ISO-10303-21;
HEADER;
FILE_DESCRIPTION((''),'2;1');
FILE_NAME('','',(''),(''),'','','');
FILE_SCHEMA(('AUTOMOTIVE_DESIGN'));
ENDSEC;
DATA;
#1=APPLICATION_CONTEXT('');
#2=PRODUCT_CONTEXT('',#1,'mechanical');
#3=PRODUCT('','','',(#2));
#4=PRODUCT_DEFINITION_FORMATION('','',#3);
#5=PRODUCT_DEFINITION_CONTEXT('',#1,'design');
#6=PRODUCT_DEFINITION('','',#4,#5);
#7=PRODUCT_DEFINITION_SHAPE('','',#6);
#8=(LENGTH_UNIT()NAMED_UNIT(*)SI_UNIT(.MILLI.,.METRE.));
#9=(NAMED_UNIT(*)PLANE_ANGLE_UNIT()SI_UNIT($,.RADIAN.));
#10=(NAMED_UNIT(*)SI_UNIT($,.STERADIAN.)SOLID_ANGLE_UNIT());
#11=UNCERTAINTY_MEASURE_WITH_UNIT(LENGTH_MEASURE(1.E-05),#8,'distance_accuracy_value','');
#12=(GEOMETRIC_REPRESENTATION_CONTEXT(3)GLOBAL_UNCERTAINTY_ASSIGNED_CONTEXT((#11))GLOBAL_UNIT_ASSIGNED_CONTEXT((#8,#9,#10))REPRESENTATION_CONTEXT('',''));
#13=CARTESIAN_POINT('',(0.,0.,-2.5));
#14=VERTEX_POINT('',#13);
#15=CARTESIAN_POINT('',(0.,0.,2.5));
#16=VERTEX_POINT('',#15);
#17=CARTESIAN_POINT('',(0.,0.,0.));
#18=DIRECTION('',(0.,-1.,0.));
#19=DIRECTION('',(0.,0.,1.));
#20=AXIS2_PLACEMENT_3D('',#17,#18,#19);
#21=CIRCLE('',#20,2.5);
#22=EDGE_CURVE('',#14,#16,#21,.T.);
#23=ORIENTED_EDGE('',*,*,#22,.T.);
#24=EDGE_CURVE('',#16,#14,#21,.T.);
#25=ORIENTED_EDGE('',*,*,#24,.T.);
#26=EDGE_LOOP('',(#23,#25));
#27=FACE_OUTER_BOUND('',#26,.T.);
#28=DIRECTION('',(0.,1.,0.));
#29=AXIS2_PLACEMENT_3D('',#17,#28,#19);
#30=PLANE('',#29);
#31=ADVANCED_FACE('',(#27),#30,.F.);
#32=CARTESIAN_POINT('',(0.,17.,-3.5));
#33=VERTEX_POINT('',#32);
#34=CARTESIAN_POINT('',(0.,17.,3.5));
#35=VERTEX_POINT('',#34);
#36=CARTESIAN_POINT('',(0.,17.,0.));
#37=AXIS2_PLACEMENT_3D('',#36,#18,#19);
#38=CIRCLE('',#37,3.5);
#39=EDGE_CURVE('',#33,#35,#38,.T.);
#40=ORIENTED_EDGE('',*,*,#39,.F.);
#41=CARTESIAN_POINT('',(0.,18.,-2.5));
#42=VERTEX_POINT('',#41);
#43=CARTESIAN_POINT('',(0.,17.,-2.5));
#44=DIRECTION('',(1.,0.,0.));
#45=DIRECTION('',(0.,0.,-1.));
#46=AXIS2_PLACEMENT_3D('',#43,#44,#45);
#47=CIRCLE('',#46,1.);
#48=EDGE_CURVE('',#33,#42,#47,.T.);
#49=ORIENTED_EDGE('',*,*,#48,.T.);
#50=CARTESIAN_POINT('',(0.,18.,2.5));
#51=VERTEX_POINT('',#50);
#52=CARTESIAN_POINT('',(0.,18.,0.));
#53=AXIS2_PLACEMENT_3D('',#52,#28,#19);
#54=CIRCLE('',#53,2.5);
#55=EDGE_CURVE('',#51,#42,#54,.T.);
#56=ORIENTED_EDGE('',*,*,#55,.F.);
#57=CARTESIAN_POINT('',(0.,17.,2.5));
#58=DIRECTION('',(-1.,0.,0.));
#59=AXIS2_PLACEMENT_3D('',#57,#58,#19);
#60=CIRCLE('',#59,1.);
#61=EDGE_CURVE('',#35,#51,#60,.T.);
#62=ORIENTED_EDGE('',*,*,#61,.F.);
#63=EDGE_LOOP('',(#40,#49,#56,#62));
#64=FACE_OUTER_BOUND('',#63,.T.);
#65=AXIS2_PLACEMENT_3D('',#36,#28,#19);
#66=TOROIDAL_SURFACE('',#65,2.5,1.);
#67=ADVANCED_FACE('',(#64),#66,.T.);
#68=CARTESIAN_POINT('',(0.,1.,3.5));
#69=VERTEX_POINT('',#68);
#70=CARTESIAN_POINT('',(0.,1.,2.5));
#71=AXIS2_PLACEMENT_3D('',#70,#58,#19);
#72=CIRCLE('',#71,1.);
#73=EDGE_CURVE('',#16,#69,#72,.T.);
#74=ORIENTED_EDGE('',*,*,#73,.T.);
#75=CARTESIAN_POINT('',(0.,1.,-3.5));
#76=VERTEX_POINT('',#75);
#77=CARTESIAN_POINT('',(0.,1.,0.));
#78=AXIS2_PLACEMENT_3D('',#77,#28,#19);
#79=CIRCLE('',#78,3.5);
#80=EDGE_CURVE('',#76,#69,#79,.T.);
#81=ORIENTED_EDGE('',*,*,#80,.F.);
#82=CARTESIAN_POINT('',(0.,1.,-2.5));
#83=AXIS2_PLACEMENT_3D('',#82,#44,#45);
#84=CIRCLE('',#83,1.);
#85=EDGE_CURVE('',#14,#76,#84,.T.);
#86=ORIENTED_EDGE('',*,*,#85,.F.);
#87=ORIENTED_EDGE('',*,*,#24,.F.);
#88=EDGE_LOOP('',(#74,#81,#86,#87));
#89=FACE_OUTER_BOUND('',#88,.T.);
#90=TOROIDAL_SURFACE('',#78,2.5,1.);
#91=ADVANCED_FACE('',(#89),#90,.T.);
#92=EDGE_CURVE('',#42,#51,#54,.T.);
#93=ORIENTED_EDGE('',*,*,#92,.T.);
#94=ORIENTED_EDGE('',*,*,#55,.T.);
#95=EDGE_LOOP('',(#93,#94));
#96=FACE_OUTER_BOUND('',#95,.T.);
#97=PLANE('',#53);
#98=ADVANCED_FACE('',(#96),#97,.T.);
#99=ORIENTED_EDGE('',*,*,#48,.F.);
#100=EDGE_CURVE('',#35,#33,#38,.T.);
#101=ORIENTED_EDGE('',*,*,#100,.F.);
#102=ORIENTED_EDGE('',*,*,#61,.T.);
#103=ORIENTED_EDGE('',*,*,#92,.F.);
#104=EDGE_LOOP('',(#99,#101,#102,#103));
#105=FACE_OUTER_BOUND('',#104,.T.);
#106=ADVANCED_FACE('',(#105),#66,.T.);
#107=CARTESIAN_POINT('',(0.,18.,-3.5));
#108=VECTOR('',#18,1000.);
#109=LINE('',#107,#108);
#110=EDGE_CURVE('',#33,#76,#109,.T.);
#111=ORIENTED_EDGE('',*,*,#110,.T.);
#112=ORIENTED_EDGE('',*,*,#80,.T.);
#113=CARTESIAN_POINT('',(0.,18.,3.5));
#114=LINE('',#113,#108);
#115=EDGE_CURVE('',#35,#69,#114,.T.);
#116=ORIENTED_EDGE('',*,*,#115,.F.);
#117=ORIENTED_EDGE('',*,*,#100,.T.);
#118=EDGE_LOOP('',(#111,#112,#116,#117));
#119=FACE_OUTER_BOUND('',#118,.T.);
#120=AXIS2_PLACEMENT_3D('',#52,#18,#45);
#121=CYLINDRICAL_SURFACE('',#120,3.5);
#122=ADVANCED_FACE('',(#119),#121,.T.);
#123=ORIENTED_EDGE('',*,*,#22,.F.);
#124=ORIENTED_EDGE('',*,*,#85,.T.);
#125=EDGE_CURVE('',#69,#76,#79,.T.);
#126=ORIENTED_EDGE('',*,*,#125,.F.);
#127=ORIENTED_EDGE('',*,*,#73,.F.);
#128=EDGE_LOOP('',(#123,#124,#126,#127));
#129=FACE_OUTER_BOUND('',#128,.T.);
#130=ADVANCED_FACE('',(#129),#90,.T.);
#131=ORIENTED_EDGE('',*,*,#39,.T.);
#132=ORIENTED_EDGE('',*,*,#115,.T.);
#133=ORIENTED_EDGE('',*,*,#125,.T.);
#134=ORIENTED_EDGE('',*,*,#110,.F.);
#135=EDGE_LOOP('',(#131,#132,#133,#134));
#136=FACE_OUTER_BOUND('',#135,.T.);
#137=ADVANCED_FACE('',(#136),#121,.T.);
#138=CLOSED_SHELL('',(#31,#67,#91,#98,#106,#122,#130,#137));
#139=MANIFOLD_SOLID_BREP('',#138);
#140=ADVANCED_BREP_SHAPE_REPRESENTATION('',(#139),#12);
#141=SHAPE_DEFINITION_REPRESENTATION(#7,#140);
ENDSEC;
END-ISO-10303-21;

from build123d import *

# Parameters (mm, degrees)
SKETCH1_R           = 3.5
BOSS_EXTRUDE1_DEPTH = 18
FILLET1_R           = 1


with BuildPart() as part:
    # Sketch1 → Boss-Extrude1 (new body)
    with BuildSketch(Plane(origin=(0, 0, 0), x_dir=(1, 0, 0), z_dir=(0, 1, 0))):
        with Locations(Location((0, 0, 0), (0, 0, 270))):
            Circle(SKETCH1_R)
    extrude(amount=BOSS_EXTRUDE1_DEPTH)

    # Fillet1
    fillet1_edges = [part.edges().sort_by_distance(p)[0] for p in [
        (0, 0, -3.5),
        (0, 18, -3.5),
    ]]
    fillet(fillet1_edges, radius=FILLET1_R)


solid = part.part
